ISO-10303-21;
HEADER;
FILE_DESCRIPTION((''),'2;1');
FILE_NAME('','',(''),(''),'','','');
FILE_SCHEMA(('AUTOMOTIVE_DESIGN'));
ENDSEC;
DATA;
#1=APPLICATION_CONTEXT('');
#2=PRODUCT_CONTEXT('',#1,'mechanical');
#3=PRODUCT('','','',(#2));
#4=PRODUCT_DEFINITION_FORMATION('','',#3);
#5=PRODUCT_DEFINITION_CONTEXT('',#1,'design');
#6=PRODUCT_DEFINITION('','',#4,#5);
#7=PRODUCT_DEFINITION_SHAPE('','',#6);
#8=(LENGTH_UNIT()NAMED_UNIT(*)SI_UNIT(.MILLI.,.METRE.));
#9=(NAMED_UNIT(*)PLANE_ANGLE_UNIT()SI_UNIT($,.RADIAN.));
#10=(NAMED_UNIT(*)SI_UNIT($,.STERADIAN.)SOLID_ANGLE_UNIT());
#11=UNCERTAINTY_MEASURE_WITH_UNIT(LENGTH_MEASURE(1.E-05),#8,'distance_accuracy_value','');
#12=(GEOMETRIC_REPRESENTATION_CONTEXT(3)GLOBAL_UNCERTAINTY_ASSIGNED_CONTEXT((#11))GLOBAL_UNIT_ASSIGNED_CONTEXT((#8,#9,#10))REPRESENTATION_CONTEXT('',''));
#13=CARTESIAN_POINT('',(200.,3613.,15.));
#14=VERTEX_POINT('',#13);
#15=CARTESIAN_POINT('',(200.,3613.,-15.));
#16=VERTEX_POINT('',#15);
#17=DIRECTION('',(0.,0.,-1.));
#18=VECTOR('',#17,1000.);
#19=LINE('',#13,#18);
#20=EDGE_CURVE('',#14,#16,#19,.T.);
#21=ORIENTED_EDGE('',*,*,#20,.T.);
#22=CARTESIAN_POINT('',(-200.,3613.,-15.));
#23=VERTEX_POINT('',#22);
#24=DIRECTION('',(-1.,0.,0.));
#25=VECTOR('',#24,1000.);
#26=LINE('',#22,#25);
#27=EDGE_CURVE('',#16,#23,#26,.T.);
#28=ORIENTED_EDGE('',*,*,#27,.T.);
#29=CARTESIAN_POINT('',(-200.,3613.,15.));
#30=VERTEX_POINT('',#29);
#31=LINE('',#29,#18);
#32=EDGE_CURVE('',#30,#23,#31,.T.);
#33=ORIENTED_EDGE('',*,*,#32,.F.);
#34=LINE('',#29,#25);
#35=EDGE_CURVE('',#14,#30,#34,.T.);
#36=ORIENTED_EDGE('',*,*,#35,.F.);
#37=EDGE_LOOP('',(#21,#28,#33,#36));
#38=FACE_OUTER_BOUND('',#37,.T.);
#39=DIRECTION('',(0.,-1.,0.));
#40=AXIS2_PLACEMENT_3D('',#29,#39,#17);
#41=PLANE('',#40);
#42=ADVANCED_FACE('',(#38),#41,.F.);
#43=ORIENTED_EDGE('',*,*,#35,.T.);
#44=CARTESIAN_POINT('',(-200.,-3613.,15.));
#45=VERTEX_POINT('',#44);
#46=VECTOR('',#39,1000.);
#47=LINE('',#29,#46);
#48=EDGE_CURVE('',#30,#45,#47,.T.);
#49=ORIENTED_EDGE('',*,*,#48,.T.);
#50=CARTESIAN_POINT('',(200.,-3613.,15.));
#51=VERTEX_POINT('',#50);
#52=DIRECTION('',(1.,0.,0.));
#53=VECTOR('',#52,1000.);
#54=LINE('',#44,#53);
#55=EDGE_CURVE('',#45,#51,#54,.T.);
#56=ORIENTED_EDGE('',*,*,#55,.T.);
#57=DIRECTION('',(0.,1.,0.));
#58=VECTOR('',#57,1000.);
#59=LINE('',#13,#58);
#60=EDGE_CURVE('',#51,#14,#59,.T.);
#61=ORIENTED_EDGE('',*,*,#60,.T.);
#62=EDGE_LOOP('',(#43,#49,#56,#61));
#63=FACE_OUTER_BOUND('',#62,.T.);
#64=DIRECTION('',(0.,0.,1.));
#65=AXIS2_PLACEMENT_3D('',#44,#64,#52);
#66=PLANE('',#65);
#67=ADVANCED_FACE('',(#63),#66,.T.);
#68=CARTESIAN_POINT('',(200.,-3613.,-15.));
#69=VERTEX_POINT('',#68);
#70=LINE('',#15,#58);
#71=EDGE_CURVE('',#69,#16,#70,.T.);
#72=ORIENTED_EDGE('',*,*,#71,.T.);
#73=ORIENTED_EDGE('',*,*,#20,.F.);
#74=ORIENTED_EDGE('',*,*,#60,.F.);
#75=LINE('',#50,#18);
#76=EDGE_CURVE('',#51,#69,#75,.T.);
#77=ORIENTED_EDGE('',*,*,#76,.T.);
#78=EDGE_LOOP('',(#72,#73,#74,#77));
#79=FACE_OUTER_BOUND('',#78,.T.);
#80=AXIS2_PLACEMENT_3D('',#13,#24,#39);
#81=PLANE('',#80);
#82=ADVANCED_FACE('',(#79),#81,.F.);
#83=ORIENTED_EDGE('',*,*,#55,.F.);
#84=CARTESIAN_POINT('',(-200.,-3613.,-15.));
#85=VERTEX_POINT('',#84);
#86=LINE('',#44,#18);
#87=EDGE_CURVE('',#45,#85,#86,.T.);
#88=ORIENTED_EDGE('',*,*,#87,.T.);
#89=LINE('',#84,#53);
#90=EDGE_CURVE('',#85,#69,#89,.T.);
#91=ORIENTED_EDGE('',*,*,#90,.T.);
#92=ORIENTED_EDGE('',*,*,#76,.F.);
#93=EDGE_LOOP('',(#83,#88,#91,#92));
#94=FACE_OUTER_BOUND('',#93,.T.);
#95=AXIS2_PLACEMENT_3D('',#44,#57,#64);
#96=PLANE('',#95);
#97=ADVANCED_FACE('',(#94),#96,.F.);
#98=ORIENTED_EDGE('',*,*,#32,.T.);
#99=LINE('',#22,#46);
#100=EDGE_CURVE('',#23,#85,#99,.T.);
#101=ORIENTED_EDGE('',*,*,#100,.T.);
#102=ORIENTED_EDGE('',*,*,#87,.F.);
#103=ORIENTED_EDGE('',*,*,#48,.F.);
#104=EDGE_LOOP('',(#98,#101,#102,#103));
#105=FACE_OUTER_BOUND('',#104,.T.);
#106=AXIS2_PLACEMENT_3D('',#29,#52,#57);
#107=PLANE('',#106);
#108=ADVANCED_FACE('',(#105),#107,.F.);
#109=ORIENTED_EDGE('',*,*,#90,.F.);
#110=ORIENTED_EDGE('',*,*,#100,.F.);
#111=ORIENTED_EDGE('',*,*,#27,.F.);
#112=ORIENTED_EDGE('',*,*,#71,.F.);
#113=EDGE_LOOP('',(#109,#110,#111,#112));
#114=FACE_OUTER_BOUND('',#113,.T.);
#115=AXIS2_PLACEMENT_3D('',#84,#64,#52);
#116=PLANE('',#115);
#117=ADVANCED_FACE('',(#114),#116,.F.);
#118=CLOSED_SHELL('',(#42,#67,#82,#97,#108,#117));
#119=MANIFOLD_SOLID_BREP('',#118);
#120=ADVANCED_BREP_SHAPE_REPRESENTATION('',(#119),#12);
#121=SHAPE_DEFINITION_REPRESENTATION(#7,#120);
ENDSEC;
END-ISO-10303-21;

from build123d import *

# Parameters (mm, degrees)
SKETCH1_W           = 400
SKETCH1_H           = 7226
BOSS_EXTRUDE1_DEPTH = 15


with BuildPart() as part:
    # Sketch1 → Boss-Extrude1 (new, symmetric)
    with BuildSketch(Plane.XY):
        Rectangle(SKETCH1_W, SKETCH1_H)
    extrude(amount=BOSS_EXTRUDE1_DEPTH, both=True)


solid = part.part
